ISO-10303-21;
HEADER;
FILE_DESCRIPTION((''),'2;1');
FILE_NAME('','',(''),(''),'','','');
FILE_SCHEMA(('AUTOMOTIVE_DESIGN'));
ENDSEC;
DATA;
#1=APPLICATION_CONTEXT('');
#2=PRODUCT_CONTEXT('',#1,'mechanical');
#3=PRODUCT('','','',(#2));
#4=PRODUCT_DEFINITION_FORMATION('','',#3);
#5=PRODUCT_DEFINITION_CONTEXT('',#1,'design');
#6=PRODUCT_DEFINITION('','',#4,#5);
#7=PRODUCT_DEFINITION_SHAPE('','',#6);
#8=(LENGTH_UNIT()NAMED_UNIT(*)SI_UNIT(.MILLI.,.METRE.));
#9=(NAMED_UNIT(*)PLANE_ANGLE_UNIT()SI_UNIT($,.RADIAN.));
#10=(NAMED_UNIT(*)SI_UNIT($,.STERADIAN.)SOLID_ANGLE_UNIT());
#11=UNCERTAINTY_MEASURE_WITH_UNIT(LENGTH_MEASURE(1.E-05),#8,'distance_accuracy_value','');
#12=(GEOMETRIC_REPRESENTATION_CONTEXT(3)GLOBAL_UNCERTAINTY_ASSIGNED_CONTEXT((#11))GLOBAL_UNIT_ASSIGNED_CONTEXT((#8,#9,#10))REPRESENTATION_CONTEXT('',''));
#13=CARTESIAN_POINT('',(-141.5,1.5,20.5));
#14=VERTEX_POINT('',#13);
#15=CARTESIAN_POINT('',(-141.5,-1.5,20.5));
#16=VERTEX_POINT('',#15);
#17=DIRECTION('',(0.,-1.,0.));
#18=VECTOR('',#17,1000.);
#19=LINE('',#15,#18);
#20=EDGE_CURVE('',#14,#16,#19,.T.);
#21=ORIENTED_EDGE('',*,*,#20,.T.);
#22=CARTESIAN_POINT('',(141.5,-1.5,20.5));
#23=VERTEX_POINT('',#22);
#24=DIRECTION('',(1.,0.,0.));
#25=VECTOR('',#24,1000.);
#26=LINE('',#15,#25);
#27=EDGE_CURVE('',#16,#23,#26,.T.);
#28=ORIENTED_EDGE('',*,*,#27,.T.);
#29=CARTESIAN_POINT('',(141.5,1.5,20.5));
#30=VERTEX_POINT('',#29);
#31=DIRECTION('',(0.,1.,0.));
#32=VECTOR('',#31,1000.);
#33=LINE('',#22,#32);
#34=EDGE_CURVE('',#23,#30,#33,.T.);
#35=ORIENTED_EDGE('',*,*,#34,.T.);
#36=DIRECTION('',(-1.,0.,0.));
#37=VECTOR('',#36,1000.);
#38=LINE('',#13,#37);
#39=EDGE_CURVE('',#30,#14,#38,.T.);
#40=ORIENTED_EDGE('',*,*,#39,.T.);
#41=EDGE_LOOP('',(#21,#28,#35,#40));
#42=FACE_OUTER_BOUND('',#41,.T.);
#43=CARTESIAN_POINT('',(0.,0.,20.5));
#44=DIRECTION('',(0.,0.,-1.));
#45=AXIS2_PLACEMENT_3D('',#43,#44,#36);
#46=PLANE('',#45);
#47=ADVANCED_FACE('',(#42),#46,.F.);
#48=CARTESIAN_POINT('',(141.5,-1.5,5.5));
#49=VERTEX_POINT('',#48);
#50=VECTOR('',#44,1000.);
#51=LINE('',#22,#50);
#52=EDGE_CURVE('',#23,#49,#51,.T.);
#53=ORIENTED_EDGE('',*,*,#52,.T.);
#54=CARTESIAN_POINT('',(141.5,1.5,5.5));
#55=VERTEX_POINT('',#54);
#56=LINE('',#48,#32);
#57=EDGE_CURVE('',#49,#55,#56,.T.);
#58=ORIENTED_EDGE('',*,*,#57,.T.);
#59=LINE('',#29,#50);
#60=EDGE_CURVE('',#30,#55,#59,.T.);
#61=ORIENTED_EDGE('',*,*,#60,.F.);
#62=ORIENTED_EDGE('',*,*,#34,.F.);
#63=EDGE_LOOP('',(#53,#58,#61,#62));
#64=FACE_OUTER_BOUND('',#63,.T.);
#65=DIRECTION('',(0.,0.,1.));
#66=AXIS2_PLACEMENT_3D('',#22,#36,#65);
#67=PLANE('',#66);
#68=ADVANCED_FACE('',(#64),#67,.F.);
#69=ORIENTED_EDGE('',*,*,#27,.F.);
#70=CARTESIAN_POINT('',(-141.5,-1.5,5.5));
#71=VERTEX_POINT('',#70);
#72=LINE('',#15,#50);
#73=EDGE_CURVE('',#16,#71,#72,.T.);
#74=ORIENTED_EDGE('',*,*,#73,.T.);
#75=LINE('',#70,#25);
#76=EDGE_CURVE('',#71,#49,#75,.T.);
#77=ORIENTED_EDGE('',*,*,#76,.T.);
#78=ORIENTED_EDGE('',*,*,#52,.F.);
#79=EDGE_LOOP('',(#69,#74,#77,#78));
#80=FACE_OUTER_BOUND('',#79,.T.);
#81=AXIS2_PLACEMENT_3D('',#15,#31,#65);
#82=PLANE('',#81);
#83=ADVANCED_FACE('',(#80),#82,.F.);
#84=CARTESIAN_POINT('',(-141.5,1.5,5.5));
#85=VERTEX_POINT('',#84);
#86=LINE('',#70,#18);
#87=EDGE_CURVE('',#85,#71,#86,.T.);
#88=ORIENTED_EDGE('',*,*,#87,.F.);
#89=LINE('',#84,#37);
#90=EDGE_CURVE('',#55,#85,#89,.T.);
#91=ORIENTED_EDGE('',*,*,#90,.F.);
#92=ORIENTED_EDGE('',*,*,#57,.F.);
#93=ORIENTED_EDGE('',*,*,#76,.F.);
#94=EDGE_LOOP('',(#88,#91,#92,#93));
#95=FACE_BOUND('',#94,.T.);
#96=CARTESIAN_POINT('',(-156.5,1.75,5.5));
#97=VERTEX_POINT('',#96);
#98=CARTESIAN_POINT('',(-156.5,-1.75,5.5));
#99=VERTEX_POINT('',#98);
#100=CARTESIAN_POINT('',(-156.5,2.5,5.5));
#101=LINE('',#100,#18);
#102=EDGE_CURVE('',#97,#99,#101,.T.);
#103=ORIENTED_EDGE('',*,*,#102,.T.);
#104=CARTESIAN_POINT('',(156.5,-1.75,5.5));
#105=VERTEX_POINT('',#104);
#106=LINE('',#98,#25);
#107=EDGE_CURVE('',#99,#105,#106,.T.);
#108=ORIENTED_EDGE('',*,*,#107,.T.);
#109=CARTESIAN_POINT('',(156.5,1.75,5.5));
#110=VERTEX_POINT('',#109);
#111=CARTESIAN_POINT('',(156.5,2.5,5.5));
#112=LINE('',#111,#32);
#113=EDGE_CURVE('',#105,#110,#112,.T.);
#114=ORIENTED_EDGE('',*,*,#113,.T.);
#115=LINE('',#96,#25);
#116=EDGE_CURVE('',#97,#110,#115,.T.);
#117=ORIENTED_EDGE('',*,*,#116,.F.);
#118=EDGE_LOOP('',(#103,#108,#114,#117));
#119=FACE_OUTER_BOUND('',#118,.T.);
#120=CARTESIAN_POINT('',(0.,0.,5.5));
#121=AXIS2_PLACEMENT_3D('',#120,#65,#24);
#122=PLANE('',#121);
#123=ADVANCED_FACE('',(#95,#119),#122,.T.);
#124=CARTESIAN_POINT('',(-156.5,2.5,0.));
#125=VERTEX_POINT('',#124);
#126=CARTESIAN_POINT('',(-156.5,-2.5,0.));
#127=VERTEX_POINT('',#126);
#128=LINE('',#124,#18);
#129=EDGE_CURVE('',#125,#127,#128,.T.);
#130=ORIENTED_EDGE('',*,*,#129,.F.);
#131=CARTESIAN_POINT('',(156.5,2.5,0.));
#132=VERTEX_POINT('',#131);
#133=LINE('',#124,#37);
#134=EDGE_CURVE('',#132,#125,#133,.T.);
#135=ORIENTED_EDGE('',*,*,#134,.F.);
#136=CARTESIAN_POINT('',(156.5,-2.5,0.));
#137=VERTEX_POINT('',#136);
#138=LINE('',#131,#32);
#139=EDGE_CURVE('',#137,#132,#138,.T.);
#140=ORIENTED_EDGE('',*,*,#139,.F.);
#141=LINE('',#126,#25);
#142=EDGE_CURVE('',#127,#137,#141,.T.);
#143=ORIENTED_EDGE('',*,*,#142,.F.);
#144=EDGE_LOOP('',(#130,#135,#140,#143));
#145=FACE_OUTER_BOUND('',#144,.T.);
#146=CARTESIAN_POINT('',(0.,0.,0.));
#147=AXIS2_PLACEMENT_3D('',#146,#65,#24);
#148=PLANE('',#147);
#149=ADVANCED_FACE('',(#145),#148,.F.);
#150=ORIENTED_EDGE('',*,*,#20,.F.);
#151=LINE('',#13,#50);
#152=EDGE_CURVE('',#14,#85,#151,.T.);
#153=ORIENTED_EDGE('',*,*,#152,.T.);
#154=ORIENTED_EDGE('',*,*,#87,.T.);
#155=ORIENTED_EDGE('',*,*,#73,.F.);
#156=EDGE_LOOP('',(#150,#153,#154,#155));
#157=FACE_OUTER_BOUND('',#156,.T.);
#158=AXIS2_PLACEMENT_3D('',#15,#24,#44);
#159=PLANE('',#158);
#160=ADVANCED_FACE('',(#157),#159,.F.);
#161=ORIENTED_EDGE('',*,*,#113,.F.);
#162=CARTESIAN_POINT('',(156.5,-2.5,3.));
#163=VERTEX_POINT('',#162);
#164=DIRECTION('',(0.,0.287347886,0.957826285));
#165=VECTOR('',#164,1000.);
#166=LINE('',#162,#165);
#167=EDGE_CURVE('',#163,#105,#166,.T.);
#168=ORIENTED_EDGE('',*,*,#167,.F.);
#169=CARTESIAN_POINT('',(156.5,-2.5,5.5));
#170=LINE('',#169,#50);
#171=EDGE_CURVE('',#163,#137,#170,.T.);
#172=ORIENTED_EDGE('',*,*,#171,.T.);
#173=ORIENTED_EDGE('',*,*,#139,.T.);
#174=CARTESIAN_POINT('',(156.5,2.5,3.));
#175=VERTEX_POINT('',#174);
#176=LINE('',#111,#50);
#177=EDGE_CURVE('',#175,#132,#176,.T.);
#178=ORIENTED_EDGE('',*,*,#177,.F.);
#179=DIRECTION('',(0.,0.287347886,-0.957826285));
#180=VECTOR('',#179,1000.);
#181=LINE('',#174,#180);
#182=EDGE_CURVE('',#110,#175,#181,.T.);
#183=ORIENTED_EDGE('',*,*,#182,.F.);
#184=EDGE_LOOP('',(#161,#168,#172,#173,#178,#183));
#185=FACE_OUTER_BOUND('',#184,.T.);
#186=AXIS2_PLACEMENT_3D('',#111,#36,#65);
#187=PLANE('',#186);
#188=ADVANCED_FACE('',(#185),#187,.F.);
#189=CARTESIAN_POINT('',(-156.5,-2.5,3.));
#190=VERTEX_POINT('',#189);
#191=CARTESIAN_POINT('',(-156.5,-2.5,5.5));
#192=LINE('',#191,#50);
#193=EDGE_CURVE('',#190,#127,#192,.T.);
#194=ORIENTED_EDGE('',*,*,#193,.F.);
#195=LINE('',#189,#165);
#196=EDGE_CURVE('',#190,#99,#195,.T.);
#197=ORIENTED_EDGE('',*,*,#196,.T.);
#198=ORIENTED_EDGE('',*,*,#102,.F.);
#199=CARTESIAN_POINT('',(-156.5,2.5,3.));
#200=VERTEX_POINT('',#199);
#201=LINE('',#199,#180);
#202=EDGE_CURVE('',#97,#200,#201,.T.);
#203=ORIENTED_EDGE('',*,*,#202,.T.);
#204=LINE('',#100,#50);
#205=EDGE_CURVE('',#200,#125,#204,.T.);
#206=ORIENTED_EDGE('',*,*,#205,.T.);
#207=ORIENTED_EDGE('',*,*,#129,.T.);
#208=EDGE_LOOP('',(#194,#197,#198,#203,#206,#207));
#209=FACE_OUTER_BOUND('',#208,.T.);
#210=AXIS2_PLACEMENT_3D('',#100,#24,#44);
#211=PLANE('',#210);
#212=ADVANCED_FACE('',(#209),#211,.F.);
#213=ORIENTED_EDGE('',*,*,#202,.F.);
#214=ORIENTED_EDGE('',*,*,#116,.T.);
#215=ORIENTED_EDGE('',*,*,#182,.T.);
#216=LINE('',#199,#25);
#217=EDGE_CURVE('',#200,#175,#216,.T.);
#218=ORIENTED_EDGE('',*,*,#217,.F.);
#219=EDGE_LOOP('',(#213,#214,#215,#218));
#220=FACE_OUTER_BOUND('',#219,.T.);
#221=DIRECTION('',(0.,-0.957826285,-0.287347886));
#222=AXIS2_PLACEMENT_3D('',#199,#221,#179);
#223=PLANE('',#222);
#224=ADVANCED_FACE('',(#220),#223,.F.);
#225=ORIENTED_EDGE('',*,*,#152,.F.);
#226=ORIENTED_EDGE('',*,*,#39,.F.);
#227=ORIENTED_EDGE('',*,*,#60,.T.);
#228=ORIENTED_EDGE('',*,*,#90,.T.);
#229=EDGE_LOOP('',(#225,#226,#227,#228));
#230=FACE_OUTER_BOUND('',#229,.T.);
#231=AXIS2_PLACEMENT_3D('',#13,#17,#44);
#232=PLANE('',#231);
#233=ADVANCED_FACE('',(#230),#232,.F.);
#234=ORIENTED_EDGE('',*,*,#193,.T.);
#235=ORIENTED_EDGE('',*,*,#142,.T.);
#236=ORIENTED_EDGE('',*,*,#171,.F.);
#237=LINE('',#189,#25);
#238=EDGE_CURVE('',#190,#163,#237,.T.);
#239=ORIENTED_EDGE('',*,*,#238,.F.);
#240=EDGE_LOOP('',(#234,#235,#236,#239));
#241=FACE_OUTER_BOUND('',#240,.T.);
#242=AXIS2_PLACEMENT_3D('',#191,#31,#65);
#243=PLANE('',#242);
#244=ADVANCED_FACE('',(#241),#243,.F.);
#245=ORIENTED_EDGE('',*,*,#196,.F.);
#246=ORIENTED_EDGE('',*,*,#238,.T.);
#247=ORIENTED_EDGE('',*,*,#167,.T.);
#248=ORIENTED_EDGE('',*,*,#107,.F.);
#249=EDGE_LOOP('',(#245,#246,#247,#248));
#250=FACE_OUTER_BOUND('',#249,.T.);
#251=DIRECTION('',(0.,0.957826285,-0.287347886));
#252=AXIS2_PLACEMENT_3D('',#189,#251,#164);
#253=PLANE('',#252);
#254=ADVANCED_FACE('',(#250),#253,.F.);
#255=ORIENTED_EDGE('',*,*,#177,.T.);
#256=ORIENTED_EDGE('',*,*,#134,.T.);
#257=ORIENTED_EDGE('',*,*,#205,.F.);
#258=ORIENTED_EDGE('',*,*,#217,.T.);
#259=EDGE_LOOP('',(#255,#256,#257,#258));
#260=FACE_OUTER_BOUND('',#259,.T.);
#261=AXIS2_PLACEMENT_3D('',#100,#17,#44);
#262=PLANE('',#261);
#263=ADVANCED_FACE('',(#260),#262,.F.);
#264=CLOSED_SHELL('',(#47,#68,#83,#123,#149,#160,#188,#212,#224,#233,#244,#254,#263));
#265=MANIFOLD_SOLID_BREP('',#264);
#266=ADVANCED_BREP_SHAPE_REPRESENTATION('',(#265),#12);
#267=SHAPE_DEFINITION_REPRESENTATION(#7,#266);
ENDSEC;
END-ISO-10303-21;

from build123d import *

# Parameters (mm, degrees)
SKETCH1_W           = 313
SKETCH1_H           = 5
BOSS_EXTRUDE1_DEPTH = 5.5
CUT_EXTRUDE1_DEPTH  = 314.058301279
SKETCH2_W           = 283
SKETCH2_H           = 3
BOSS_EXTRUDE2_DEPTH = 15


with BuildPart() as part:
    # Sketch1 → Boss-Extrude1 (new body)
    with BuildSketch(Plane.XY):
        Rectangle(SKETCH1_W, SKETCH1_H)
    extrude(amount=BOSS_EXTRUDE1_DEPTH)

    # Sketch3 → Cut-Extrude1 (cut, through all)
    with BuildSketch(Plane(origin=(156.5, 0, 0), x_dir=(0, 0, -1), z_dir=(1, 0, 0))):
        Polygon((-3, 2.5), (-5.5, 1.75), (-5.5, 2.5), align=None)
        Polygon((-3, -2.5), (-5.5, -1.75), (-5.5, -2.5), align=None)
    extrude(amount=-CUT_EXTRUDE1_DEPTH, mode=Mode.SUBTRACT)

    # Sketch2 → Boss-Extrude2 (add)
    with BuildSketch(Plane.XY.offset(5.5)):
        Rectangle(SKETCH2_W, SKETCH2_H)
    extrude(amount=BOSS_EXTRUDE2_DEPTH)


solid = part.part
